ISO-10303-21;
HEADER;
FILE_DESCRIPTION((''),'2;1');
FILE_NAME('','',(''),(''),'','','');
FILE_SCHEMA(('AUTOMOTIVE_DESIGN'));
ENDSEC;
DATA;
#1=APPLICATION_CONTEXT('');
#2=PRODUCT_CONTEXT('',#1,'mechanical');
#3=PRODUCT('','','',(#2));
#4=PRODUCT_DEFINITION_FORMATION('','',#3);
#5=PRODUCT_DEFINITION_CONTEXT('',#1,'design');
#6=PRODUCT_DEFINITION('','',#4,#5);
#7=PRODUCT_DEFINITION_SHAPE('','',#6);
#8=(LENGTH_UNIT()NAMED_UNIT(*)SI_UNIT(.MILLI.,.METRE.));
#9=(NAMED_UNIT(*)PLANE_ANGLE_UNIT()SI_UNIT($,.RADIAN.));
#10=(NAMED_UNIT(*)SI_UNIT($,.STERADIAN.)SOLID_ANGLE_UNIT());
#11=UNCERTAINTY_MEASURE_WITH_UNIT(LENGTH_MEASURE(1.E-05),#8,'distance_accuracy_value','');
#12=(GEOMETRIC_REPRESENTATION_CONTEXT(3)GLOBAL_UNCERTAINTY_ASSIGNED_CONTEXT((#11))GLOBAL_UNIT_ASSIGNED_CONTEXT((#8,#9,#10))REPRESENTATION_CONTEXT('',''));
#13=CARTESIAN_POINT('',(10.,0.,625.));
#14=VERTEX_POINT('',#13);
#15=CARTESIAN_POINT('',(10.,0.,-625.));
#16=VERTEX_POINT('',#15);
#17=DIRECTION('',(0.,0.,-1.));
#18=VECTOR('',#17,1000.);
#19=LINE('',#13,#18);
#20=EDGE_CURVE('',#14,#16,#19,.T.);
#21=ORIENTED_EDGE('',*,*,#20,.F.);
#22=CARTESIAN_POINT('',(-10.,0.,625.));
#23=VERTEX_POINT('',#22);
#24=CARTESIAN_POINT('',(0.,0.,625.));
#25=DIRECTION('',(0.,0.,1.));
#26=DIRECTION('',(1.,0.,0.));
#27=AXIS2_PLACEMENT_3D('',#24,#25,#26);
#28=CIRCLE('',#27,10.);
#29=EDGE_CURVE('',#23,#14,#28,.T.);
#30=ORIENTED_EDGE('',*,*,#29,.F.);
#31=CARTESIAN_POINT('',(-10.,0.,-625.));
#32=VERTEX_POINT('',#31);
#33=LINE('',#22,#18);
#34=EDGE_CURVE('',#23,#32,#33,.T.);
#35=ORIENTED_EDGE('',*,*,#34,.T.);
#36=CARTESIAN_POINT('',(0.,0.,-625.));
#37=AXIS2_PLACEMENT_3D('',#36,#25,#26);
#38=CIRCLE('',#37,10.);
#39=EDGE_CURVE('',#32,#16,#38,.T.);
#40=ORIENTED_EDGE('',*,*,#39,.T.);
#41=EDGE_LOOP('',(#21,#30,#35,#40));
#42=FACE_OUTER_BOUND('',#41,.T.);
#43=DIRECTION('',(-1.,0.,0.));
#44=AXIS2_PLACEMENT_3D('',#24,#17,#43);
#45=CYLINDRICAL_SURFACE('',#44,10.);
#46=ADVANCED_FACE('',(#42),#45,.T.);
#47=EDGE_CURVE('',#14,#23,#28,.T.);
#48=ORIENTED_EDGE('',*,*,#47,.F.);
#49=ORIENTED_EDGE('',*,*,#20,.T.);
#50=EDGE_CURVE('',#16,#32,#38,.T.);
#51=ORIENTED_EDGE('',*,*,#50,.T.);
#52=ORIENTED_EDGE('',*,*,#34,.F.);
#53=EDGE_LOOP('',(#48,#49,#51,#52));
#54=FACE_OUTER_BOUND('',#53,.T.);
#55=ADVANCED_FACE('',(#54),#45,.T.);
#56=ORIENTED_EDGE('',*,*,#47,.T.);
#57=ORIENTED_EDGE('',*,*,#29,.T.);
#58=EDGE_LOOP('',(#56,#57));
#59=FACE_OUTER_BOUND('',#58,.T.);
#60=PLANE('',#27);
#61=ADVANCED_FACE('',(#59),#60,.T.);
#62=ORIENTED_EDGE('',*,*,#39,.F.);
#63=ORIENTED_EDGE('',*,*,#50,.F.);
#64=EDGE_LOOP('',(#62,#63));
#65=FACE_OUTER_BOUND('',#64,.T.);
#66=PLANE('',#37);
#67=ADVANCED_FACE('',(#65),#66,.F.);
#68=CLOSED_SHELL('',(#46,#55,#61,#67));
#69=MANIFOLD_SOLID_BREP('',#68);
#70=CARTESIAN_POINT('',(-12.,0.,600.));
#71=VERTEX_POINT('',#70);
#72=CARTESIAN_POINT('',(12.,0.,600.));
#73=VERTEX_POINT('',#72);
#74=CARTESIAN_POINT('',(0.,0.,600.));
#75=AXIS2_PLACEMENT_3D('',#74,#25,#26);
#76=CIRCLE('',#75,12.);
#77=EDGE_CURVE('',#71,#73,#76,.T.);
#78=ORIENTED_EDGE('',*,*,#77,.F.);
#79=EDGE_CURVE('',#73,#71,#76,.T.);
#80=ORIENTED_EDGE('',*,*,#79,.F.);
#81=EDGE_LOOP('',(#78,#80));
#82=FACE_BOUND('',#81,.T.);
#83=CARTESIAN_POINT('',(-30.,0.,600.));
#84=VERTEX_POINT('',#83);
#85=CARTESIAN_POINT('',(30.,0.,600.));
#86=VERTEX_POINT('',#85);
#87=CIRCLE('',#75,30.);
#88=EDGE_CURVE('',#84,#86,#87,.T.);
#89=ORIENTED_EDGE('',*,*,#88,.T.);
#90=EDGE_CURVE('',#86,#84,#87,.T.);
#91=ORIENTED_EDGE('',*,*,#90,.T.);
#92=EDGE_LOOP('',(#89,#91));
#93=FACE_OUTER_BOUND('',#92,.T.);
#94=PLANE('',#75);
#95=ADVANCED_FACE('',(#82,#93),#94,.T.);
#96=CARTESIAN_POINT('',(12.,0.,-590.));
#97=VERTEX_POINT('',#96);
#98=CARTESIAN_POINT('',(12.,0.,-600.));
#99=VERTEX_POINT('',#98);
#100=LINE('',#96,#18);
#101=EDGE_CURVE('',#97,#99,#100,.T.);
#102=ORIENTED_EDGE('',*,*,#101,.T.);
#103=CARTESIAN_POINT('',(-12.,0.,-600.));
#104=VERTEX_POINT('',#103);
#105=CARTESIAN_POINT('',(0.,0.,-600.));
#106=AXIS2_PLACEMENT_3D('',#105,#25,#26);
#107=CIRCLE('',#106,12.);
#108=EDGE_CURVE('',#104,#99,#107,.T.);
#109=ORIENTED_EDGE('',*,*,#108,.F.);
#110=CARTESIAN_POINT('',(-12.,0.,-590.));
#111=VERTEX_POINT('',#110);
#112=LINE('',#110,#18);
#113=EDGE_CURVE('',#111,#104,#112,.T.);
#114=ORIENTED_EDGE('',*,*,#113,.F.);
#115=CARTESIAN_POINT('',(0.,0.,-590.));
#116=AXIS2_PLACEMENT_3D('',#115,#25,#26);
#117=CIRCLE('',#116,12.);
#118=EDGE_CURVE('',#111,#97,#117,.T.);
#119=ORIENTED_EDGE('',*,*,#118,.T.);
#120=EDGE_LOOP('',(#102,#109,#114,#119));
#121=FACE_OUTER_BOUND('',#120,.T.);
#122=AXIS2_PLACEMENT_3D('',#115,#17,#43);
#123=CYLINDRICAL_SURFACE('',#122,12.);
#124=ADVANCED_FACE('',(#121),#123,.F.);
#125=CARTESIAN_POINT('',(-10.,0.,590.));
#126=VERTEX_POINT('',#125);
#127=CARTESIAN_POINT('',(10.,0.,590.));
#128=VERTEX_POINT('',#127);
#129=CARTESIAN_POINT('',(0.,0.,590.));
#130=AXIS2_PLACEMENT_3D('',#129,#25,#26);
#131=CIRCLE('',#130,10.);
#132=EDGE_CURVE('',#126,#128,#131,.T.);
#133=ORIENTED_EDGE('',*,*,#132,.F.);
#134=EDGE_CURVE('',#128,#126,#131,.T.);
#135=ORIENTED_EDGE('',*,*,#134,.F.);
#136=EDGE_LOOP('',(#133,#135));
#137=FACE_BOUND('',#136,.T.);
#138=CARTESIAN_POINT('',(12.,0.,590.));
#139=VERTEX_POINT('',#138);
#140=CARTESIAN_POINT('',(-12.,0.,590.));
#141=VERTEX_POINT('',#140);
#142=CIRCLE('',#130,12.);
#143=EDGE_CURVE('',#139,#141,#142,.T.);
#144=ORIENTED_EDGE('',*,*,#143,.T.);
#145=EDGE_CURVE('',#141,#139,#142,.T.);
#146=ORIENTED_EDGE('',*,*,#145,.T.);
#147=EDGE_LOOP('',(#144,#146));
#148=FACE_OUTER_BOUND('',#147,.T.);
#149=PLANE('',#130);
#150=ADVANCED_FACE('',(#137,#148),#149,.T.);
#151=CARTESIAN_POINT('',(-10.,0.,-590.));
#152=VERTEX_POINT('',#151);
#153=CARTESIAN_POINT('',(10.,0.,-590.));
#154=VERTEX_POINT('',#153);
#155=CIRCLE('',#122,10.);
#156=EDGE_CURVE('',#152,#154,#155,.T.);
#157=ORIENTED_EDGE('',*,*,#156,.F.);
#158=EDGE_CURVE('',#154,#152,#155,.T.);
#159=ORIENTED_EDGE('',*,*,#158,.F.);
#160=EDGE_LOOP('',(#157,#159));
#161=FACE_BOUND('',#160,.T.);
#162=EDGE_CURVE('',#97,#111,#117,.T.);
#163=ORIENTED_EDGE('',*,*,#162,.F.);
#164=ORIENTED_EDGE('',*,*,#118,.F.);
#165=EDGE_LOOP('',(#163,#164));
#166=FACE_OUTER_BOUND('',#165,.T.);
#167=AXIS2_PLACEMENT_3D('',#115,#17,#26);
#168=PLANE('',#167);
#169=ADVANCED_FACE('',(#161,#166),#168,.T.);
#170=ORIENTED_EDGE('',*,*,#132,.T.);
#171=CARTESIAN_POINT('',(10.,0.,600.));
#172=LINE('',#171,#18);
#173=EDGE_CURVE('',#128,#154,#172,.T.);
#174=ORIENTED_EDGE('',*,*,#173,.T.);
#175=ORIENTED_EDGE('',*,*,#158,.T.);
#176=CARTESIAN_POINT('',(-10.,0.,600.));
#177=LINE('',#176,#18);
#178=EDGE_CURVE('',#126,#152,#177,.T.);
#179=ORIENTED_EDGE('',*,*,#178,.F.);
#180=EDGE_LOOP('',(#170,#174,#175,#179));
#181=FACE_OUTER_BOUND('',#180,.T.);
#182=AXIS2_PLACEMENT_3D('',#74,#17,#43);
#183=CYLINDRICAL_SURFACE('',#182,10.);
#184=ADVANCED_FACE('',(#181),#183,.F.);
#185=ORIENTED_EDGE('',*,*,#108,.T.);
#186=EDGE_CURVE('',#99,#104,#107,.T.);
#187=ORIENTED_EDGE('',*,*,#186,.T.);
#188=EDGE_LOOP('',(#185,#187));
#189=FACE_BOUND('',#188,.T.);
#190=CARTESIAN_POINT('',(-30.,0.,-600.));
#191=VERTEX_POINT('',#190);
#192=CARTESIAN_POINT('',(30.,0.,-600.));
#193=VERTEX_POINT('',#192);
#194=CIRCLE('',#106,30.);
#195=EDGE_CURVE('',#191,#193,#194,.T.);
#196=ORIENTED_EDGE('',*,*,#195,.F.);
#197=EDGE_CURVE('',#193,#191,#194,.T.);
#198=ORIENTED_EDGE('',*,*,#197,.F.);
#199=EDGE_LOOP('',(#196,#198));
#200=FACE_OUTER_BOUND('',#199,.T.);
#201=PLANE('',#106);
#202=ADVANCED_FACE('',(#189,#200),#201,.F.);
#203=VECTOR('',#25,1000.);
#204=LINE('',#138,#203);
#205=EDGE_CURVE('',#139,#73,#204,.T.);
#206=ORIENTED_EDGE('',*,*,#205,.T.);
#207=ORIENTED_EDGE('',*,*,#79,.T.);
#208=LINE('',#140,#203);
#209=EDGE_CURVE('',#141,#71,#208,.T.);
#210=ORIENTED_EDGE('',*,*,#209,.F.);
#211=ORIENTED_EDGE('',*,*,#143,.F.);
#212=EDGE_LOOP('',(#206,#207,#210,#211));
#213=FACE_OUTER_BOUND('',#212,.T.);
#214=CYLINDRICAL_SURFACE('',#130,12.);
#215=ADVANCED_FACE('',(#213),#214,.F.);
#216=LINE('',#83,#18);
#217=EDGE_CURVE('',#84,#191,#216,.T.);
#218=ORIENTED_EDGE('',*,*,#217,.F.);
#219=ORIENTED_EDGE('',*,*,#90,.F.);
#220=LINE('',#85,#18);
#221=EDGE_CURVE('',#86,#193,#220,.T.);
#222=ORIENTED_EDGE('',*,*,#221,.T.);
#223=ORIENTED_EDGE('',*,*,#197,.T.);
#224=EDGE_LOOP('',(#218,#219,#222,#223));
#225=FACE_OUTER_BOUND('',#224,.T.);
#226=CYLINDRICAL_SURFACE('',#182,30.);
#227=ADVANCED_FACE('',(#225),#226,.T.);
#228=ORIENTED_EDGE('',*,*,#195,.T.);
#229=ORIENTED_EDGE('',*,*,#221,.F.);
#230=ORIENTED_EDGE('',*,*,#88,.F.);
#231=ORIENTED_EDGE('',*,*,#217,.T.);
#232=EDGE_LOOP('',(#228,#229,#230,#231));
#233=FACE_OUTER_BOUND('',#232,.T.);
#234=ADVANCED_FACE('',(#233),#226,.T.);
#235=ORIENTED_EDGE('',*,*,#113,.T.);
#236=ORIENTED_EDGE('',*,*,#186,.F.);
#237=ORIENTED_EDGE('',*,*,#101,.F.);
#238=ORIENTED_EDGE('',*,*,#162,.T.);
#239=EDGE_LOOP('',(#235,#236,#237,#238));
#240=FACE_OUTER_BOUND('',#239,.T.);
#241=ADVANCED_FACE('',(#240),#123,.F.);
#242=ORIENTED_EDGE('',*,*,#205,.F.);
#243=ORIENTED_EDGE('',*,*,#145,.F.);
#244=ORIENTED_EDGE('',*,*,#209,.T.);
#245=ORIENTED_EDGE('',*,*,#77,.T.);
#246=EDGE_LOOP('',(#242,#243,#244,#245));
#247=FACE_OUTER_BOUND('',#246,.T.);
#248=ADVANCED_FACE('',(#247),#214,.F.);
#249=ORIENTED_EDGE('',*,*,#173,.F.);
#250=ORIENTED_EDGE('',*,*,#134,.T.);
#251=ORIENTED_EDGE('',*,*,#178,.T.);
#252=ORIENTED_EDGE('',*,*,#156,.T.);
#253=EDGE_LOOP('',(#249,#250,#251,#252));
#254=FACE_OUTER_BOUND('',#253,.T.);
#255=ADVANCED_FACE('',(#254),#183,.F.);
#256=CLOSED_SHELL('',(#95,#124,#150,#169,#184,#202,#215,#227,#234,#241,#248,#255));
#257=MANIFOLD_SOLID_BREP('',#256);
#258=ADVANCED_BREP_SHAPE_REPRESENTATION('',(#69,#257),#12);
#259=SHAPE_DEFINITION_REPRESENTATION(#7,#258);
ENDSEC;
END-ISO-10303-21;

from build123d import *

# Parameters (mm, degrees)
SKETCH_1_R          = 10
EXTRUDE_1_DEPTH     = 625
SKETCH_2_R          = 30
SKETCH_2_R_2        = 10
EXTRUDE_2_DEPTH     = 600
SKETCH_3_R          = 12
SKETCH_3_R_2        = 5
CUT_EXTRUDE_1_DEPTH = 10


with BuildPart() as part:
    # 草图1 → 凸台-拉伸1 (new, symmetric)
    with BuildSketch(Plane.XY):
        Circle(SKETCH_1_R)
    extrude(amount=EXTRUDE_1_DEPTH, both=True)


with BuildPart() as body_2:
    # 草图2 → 凸台-拉伸2 (new, symmetric)
    with BuildSketch(Plane.XY):
        Circle(SKETCH_2_R)
        Circle(SKETCH_2_R_2, mode=Mode.SUBTRACT)
    extrude(amount=EXTRUDE_2_DEPTH, both=True)

    # 草图3 → 切除-拉伸1 (cut)
    with BuildSketch(Plane.XY.offset(600)):
        Circle(SKETCH_3_R)
        Circle(SKETCH_3_R_2, mode=Mode.SUBTRACT)
    cut_extrude_1 = extrude(amount=-CUT_EXTRUDE_1_DEPTH, mode=Mode.SUBTRACT)

    # 镜向1: 切除-拉伸1 across plane
    add(cut_extrude_1.mirror(Plane.XY), mode=Mode.SUBTRACT)


solid = Compound([part.part, body_2.part])
